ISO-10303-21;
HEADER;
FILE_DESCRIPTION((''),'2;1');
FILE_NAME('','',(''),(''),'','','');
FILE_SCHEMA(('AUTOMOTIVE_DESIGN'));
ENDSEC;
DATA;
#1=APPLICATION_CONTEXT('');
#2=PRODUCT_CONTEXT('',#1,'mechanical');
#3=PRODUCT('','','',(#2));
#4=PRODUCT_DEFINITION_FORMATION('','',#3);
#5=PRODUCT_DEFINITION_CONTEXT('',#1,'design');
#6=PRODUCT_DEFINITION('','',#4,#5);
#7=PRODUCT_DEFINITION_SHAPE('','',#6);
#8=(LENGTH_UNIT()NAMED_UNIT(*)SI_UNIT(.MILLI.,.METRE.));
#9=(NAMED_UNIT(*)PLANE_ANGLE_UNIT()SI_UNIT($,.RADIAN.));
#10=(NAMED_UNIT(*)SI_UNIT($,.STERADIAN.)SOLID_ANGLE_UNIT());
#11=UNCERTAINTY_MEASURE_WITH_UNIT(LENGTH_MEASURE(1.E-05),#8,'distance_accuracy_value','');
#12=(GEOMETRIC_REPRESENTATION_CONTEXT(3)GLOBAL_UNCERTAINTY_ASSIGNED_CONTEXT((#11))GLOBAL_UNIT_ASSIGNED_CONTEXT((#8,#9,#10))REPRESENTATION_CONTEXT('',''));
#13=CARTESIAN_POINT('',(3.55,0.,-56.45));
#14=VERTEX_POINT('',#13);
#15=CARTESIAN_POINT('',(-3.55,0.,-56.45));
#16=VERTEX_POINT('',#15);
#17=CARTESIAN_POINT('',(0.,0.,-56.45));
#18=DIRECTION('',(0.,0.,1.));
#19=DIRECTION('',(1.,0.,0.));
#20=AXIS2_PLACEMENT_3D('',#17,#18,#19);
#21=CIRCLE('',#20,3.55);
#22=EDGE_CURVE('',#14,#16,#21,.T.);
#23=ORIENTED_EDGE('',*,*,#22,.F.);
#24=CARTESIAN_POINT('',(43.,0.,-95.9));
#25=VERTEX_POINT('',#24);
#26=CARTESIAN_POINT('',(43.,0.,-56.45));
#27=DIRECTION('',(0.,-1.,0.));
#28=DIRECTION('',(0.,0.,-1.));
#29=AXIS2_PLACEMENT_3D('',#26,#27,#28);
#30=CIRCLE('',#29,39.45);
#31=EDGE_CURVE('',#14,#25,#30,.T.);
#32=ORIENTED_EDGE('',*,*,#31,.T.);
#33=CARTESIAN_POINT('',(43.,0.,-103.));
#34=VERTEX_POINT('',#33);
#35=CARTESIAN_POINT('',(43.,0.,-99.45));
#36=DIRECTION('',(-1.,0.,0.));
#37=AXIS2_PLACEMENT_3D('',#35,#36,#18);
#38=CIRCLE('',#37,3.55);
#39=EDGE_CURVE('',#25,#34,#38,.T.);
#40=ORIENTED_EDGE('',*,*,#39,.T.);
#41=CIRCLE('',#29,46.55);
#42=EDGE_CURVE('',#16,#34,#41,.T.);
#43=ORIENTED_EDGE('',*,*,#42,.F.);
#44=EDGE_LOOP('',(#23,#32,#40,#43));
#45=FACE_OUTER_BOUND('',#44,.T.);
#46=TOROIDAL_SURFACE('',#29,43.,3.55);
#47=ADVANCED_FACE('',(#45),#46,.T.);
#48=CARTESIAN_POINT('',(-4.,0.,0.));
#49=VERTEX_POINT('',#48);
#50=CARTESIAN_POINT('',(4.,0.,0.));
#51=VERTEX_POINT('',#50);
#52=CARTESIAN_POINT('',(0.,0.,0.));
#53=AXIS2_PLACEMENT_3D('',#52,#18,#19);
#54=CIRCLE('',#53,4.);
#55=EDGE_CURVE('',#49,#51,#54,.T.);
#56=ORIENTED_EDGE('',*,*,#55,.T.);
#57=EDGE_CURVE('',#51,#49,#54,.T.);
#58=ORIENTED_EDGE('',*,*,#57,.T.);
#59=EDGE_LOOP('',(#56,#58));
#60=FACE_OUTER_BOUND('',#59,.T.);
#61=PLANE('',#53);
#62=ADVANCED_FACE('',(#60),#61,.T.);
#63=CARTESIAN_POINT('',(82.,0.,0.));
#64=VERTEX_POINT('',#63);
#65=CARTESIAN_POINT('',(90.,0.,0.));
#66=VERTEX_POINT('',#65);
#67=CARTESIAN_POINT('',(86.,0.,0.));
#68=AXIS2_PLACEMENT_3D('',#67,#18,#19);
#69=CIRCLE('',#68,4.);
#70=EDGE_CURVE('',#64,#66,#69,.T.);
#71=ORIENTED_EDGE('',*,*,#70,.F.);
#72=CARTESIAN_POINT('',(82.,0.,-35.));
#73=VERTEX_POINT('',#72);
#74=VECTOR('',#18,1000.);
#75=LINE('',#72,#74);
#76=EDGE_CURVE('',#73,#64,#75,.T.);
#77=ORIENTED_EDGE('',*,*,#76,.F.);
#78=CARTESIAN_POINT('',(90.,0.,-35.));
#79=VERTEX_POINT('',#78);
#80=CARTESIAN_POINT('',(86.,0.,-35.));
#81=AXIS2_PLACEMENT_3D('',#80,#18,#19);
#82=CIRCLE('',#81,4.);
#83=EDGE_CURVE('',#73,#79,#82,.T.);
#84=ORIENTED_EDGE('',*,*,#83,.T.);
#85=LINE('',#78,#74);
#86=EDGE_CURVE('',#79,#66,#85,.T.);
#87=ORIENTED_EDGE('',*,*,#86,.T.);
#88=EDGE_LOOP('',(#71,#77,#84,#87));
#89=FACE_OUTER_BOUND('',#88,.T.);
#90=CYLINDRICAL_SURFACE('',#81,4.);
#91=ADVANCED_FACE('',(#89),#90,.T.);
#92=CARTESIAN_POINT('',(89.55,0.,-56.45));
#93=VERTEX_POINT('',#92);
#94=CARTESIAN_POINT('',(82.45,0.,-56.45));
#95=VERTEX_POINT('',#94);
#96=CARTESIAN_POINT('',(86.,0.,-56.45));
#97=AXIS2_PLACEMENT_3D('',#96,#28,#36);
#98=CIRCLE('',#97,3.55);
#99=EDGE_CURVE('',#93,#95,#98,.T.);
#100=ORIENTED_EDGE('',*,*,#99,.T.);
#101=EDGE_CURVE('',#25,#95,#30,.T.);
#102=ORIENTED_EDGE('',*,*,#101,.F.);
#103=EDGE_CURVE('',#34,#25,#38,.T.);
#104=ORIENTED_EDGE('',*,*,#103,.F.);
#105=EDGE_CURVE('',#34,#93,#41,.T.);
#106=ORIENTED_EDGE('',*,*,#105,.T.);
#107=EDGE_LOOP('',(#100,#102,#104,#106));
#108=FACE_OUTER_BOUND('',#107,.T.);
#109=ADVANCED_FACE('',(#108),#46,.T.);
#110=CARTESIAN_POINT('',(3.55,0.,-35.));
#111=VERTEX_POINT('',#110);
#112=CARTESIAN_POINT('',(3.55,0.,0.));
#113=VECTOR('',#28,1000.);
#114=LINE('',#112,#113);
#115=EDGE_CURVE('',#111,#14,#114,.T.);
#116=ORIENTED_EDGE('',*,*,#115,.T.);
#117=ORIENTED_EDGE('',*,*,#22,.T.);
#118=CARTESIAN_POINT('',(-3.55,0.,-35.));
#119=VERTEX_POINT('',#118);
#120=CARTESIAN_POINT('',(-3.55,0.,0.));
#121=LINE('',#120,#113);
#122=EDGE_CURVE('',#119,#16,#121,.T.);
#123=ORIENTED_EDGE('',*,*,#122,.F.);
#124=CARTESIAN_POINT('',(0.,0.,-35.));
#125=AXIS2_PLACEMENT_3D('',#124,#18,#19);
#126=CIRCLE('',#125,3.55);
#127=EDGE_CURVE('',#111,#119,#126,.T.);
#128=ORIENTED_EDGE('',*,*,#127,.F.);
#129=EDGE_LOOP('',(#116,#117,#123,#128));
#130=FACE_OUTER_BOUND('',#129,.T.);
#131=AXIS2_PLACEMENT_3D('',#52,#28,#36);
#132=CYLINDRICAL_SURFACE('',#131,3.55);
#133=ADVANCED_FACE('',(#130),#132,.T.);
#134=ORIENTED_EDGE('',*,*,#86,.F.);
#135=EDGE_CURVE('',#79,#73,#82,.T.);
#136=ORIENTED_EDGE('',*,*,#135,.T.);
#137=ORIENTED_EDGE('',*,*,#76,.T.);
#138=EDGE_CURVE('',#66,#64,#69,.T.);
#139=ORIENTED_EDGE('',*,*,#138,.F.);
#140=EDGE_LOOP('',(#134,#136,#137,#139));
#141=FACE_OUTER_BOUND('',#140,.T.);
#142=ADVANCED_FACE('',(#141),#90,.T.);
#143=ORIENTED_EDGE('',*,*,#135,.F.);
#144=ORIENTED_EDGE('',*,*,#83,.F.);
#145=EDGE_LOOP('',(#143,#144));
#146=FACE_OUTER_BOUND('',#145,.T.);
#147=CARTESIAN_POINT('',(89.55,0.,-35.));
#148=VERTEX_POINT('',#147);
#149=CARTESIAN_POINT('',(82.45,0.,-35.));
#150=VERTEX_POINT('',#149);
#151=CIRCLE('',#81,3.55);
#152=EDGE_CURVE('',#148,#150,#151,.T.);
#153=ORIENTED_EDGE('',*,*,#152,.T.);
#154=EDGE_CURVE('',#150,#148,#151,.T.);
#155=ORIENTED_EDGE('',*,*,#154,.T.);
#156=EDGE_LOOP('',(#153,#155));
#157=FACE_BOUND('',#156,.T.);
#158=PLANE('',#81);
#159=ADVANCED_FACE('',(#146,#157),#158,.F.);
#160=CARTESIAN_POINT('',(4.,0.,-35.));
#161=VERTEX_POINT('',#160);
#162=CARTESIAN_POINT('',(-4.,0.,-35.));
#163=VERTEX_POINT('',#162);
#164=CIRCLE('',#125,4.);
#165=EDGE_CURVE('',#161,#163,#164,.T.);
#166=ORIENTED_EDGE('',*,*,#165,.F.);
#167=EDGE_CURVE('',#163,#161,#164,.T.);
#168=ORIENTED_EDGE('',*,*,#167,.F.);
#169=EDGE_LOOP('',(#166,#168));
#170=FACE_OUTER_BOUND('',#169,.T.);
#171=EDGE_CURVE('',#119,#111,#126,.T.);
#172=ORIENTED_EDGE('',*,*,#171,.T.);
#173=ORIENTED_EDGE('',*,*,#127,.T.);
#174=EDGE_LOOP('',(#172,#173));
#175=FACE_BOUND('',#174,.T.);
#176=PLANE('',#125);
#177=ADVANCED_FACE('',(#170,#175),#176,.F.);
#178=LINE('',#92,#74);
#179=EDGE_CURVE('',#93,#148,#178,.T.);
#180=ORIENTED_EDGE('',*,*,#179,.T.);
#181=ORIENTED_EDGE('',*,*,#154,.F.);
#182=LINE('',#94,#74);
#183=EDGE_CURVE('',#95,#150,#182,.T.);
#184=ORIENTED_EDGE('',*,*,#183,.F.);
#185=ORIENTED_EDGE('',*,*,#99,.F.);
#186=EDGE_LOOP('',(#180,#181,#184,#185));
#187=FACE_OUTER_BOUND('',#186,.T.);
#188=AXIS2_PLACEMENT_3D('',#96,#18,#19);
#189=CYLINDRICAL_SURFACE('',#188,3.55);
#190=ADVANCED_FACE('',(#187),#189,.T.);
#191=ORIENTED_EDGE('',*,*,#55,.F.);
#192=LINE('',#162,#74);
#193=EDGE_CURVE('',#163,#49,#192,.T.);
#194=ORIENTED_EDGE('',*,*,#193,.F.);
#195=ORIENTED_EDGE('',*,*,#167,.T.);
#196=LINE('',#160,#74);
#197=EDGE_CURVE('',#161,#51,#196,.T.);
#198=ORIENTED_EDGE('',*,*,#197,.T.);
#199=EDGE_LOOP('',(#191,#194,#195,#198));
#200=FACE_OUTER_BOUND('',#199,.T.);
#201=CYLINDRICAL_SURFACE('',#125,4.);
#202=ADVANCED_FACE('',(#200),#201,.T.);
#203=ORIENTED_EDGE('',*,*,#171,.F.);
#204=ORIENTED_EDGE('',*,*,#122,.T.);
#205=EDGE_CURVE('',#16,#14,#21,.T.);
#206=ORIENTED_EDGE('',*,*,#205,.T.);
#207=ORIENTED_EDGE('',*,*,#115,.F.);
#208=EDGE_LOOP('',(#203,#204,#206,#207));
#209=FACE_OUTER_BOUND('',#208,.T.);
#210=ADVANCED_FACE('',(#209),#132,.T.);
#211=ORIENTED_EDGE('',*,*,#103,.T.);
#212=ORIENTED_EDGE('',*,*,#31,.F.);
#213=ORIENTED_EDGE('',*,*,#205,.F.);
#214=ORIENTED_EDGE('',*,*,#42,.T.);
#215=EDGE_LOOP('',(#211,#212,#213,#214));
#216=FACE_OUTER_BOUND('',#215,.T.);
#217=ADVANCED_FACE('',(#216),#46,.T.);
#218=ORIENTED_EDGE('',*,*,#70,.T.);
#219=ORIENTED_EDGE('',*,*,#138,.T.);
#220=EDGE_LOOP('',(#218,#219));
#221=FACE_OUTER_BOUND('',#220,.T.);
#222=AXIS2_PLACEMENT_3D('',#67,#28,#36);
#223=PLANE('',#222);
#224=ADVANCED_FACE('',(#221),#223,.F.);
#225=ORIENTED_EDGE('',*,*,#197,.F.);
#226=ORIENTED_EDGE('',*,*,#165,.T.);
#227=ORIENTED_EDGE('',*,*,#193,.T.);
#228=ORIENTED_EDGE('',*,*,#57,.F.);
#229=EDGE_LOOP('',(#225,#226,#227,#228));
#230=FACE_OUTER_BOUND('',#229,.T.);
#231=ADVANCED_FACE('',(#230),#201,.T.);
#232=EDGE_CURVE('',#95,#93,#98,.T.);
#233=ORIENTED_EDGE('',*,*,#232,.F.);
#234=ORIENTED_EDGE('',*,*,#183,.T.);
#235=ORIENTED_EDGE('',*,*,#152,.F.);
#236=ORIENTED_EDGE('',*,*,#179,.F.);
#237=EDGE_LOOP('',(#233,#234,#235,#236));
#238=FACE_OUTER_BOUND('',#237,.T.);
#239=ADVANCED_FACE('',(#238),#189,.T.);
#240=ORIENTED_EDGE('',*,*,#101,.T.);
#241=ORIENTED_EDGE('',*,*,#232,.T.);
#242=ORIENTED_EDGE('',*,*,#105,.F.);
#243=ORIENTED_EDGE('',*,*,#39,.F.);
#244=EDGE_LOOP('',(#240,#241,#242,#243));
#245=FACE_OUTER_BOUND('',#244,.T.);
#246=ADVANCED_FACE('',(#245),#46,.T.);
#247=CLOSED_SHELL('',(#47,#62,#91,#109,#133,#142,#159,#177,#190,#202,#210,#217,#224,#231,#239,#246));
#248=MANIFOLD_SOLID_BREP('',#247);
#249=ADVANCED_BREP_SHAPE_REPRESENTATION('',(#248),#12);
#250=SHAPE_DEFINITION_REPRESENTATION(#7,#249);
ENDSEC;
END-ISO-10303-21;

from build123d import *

# Parameters (mm, degrees)
SKETCH_1_R      = 3.55
SKETCH_3_R      = 4
EXTRUDE_1_DEPTH = 35


with BuildPart() as part:
    # 扫描1: sweep along a path in 草图2
    with BuildLine(Plane(origin=(0, 0, 0), x_dir=(1, 0, 0), z_dir=(0, 1, 0))) as sweep_1_path:
        Line((0, 0), (0, 56.45))
        ThreePointArc((0, 56.45), (43, 99.45), (86, 56.45))
        Line((86, 56.45), (86, 0))
    # 草图1 → 扫描1 (sweep)
    with BuildSketch(Plane.XY):
        Circle(SKETCH_1_R)
    sweep(path=sweep_1_path.line)

    # 草图3 → 凸台-拉伸1 (add)
    with BuildSketch(Plane.XY):
        Circle(SKETCH_3_R)
        with Locations((86, 0)):
            Circle(SKETCH_3_R)
    extrude(amount=-EXTRUDE_1_DEPTH)


solid = part.part
